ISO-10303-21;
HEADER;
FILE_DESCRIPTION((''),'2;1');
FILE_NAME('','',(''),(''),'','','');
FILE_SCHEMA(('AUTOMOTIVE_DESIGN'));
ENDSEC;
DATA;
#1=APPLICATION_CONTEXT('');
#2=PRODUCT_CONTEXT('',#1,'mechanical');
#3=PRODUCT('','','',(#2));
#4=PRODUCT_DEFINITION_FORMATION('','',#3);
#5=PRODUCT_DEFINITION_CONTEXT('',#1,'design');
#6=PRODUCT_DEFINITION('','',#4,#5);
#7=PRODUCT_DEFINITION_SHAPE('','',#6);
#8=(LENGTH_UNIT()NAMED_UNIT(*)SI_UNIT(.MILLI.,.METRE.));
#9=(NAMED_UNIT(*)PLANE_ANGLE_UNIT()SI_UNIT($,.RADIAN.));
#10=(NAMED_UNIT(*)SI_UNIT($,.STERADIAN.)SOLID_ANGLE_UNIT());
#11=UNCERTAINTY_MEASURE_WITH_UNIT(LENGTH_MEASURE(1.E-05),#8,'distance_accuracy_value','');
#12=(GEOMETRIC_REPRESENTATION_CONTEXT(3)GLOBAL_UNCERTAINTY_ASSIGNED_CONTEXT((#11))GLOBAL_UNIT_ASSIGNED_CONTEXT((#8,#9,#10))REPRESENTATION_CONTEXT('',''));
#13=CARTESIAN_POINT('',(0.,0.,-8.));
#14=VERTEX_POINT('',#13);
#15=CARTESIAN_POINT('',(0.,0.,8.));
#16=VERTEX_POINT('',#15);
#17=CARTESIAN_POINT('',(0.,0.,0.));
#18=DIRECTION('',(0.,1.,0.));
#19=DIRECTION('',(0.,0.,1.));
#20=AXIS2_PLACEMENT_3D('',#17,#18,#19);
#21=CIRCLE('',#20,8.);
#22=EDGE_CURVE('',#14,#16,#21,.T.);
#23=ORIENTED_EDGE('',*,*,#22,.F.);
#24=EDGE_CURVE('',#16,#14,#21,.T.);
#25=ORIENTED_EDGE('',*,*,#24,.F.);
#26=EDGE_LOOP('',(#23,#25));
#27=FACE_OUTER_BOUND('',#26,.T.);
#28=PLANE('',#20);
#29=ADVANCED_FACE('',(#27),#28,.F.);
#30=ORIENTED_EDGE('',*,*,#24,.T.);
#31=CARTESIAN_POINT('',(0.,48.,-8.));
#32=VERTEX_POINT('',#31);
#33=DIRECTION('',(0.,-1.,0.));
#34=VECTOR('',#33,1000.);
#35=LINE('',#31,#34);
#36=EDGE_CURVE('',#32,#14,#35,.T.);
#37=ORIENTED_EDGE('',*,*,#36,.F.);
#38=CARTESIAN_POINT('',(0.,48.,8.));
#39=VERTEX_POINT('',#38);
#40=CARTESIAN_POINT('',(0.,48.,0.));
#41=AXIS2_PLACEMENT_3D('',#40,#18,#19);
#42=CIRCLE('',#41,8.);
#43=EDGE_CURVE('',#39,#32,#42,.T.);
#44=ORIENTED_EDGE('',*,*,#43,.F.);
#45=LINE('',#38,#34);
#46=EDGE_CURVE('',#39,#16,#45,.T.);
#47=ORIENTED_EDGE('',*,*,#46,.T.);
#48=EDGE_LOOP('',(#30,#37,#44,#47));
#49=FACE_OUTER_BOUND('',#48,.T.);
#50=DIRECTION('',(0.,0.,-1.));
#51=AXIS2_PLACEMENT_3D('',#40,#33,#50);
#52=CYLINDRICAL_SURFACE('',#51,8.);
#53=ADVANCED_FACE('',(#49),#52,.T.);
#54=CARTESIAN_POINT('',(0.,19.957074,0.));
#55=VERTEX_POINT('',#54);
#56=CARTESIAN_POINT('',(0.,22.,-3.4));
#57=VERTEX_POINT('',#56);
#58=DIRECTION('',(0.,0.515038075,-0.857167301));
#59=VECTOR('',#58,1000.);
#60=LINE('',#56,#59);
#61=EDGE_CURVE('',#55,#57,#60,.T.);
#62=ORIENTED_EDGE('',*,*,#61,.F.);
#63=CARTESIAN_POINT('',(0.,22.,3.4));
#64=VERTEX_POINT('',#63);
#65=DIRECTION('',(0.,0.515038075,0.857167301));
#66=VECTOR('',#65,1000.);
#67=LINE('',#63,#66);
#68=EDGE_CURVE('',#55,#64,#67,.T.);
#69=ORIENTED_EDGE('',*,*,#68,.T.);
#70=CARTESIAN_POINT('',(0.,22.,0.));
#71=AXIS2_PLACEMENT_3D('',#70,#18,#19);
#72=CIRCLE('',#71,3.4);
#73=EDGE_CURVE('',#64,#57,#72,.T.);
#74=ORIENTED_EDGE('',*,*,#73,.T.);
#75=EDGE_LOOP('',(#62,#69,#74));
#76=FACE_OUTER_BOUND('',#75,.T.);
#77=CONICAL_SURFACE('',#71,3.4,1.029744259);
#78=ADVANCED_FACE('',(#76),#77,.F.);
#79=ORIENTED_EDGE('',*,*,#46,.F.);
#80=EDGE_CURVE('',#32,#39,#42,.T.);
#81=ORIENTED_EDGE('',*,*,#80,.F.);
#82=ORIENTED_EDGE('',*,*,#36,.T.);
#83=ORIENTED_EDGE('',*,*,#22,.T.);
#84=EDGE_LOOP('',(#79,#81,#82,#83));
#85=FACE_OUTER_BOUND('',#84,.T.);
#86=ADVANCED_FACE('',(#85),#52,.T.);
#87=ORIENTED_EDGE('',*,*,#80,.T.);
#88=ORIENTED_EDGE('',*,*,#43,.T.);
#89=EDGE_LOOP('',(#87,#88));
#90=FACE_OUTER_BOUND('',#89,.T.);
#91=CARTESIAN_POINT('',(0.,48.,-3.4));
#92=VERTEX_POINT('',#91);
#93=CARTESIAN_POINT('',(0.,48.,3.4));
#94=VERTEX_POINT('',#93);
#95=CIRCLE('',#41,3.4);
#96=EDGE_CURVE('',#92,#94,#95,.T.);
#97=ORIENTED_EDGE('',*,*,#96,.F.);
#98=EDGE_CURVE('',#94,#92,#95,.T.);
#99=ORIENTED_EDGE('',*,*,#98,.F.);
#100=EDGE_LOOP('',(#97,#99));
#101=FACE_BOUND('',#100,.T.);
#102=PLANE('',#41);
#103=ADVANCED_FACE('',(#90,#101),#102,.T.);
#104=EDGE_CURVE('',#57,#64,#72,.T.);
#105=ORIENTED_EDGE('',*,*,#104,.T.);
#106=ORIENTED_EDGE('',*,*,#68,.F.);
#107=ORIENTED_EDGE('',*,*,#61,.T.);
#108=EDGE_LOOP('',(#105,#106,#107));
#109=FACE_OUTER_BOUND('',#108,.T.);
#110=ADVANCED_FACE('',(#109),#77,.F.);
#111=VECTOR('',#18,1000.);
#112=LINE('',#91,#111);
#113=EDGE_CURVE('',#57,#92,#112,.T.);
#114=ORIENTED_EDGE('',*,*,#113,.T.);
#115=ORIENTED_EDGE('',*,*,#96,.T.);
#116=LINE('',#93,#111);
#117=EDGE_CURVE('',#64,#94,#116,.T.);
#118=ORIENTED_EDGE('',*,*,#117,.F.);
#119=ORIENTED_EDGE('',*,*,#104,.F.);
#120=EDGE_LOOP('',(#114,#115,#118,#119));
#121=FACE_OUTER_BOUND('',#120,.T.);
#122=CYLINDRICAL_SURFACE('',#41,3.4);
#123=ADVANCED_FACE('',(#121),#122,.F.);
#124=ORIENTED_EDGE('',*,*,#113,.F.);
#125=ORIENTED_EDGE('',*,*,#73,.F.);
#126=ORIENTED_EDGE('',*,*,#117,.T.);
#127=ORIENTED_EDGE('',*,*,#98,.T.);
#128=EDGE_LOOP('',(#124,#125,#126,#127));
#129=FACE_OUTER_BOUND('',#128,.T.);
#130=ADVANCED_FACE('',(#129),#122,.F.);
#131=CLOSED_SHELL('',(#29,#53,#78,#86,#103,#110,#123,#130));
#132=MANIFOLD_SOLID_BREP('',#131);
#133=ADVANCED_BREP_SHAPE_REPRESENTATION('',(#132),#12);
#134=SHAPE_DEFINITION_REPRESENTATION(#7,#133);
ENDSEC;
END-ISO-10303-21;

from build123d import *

# Parameters (mm, degrees)
SKETCH1_R             = 8
BOSS_EXTRUDE1_DEPTH   = 48
M8_TAPPED_HOLE1_D     = 6.8
M8_TAPPED_HOLE1_DEPTH = 26
M8_TAPPED_HOLE1_TIP   = 2.042926105


with BuildPart() as part:
    # Sketch1 → Boss-Extrude1 (new body)
    with BuildSketch(Plane(origin=(0, 0, 0), x_dir=(1, 0, 0), z_dir=(0, 1, 0))):
        with Locations(Location((0, 0, 0), (0, 0, 270))):
            Circle(SKETCH1_R)
    extrude(amount=BOSS_EXTRUDE1_DEPTH)

    # M8 Tapped Hole1
    with Locations(Plane(origin=(0, 48, 0), x_dir=(1, 0, 0), z_dir=(0, 1, 0))):
        with Locations((0, 0)):
            Hole(M8_TAPPED_HOLE1_D / 2, depth=M8_TAPPED_HOLE1_DEPTH)
            with Locations((0, 0, -(M8_TAPPED_HOLE1_DEPTH + M8_TAPPED_HOLE1_TIP / 2))):  # 118° drill point
                Cone(0, M8_TAPPED_HOLE1_D / 2, M8_TAPPED_HOLE1_TIP, mode=Mode.SUBTRACT)


solid = part.part
